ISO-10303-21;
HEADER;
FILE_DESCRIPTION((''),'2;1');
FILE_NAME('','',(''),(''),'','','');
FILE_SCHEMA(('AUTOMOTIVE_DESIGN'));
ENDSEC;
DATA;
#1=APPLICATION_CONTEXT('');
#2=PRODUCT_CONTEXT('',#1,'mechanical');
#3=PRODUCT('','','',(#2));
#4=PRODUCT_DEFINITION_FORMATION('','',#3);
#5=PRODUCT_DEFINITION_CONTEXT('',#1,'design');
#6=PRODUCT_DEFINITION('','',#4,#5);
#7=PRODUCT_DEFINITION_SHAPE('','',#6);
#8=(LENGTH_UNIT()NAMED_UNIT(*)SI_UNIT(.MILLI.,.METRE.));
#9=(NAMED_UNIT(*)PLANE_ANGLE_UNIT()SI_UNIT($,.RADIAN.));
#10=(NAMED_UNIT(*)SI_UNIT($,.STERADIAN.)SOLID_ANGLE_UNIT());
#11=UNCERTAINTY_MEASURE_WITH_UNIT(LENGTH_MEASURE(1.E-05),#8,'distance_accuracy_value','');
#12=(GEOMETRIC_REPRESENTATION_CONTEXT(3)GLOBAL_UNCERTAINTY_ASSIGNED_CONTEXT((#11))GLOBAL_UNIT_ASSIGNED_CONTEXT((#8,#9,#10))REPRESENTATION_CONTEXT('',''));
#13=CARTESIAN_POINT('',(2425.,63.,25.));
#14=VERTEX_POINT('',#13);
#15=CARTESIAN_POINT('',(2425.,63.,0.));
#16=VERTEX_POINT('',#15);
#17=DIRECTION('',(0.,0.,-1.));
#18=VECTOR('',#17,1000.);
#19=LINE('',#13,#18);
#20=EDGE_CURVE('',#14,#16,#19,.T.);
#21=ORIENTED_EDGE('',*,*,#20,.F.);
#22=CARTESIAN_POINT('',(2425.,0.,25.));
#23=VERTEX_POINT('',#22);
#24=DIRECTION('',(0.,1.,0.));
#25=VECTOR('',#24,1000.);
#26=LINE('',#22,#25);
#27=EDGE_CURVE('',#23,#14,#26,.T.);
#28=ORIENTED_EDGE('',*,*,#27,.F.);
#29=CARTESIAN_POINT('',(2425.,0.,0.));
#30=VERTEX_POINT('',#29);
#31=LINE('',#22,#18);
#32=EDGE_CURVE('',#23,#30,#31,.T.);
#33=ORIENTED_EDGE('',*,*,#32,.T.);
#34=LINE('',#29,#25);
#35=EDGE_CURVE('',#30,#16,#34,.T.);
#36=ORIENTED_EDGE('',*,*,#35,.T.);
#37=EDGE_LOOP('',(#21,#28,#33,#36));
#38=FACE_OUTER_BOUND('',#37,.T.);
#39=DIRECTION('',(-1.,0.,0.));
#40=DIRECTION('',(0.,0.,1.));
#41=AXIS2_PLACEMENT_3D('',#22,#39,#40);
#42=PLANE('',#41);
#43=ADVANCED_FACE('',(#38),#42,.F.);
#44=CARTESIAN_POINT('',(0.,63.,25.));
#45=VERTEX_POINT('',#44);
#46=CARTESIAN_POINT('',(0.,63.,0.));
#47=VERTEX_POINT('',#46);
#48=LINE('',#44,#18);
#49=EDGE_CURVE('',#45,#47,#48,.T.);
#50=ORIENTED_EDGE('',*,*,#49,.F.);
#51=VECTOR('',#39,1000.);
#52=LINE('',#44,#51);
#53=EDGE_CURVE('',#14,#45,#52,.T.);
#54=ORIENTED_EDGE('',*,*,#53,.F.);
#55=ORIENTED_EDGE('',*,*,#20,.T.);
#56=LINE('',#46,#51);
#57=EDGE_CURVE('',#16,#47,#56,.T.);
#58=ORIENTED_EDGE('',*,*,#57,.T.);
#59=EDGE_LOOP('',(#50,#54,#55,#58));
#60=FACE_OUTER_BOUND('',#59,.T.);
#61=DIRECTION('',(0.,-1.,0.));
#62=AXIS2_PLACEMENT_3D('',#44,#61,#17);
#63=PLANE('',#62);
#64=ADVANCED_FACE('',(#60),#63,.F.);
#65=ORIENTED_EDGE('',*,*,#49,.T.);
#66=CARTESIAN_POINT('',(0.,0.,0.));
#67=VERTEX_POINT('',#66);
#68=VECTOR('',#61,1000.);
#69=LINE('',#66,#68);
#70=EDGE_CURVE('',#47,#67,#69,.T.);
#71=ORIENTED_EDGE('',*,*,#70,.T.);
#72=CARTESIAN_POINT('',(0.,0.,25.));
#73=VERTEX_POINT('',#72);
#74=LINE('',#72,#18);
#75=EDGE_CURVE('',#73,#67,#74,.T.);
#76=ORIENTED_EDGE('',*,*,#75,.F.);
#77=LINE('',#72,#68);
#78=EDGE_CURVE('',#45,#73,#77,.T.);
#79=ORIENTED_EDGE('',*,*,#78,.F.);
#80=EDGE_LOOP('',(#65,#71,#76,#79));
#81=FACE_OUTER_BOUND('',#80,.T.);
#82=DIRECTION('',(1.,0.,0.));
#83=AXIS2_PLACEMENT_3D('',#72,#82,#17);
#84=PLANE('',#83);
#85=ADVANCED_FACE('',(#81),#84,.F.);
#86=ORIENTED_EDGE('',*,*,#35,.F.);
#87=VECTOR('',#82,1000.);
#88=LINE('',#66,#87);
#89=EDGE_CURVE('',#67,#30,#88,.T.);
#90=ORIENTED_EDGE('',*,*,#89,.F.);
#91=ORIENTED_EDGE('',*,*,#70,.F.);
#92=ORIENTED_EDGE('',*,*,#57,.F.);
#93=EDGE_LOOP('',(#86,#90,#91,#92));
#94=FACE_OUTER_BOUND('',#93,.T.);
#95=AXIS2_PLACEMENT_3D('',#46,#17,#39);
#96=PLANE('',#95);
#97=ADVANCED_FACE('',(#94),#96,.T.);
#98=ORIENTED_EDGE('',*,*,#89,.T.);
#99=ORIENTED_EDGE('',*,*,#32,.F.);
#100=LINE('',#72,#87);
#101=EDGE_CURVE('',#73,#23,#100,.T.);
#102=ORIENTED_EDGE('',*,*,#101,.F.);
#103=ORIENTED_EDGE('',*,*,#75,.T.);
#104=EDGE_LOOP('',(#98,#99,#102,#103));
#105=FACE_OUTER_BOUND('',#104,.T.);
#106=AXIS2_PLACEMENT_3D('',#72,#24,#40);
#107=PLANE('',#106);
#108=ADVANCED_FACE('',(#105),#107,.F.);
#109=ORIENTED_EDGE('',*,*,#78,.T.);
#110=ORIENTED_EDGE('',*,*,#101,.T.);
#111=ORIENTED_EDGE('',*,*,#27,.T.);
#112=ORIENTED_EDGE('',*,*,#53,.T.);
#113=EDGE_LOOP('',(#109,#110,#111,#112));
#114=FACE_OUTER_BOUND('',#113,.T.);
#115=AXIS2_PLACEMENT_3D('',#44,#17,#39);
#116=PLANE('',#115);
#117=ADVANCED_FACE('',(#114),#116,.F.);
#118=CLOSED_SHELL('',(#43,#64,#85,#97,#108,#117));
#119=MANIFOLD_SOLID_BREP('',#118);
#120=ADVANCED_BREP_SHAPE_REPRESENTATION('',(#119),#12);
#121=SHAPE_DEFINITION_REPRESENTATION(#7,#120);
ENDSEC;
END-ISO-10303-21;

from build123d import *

# Parameters (mm, degrees)
SKETCH1_W           = 2425
SKETCH1_H           = 63
BOSS_EXTRUDE1_DEPTH = 25


with BuildPart() as part:
    # Sketch1 → Boss-Extrude1 (new body)
    with BuildSketch(Plane.XY):
        with Locations((1212.5, 31.5)):
            Rectangle(SKETCH1_W, SKETCH1_H)
    extrude(amount=BOSS_EXTRUDE1_DEPTH)


solid = part.part
